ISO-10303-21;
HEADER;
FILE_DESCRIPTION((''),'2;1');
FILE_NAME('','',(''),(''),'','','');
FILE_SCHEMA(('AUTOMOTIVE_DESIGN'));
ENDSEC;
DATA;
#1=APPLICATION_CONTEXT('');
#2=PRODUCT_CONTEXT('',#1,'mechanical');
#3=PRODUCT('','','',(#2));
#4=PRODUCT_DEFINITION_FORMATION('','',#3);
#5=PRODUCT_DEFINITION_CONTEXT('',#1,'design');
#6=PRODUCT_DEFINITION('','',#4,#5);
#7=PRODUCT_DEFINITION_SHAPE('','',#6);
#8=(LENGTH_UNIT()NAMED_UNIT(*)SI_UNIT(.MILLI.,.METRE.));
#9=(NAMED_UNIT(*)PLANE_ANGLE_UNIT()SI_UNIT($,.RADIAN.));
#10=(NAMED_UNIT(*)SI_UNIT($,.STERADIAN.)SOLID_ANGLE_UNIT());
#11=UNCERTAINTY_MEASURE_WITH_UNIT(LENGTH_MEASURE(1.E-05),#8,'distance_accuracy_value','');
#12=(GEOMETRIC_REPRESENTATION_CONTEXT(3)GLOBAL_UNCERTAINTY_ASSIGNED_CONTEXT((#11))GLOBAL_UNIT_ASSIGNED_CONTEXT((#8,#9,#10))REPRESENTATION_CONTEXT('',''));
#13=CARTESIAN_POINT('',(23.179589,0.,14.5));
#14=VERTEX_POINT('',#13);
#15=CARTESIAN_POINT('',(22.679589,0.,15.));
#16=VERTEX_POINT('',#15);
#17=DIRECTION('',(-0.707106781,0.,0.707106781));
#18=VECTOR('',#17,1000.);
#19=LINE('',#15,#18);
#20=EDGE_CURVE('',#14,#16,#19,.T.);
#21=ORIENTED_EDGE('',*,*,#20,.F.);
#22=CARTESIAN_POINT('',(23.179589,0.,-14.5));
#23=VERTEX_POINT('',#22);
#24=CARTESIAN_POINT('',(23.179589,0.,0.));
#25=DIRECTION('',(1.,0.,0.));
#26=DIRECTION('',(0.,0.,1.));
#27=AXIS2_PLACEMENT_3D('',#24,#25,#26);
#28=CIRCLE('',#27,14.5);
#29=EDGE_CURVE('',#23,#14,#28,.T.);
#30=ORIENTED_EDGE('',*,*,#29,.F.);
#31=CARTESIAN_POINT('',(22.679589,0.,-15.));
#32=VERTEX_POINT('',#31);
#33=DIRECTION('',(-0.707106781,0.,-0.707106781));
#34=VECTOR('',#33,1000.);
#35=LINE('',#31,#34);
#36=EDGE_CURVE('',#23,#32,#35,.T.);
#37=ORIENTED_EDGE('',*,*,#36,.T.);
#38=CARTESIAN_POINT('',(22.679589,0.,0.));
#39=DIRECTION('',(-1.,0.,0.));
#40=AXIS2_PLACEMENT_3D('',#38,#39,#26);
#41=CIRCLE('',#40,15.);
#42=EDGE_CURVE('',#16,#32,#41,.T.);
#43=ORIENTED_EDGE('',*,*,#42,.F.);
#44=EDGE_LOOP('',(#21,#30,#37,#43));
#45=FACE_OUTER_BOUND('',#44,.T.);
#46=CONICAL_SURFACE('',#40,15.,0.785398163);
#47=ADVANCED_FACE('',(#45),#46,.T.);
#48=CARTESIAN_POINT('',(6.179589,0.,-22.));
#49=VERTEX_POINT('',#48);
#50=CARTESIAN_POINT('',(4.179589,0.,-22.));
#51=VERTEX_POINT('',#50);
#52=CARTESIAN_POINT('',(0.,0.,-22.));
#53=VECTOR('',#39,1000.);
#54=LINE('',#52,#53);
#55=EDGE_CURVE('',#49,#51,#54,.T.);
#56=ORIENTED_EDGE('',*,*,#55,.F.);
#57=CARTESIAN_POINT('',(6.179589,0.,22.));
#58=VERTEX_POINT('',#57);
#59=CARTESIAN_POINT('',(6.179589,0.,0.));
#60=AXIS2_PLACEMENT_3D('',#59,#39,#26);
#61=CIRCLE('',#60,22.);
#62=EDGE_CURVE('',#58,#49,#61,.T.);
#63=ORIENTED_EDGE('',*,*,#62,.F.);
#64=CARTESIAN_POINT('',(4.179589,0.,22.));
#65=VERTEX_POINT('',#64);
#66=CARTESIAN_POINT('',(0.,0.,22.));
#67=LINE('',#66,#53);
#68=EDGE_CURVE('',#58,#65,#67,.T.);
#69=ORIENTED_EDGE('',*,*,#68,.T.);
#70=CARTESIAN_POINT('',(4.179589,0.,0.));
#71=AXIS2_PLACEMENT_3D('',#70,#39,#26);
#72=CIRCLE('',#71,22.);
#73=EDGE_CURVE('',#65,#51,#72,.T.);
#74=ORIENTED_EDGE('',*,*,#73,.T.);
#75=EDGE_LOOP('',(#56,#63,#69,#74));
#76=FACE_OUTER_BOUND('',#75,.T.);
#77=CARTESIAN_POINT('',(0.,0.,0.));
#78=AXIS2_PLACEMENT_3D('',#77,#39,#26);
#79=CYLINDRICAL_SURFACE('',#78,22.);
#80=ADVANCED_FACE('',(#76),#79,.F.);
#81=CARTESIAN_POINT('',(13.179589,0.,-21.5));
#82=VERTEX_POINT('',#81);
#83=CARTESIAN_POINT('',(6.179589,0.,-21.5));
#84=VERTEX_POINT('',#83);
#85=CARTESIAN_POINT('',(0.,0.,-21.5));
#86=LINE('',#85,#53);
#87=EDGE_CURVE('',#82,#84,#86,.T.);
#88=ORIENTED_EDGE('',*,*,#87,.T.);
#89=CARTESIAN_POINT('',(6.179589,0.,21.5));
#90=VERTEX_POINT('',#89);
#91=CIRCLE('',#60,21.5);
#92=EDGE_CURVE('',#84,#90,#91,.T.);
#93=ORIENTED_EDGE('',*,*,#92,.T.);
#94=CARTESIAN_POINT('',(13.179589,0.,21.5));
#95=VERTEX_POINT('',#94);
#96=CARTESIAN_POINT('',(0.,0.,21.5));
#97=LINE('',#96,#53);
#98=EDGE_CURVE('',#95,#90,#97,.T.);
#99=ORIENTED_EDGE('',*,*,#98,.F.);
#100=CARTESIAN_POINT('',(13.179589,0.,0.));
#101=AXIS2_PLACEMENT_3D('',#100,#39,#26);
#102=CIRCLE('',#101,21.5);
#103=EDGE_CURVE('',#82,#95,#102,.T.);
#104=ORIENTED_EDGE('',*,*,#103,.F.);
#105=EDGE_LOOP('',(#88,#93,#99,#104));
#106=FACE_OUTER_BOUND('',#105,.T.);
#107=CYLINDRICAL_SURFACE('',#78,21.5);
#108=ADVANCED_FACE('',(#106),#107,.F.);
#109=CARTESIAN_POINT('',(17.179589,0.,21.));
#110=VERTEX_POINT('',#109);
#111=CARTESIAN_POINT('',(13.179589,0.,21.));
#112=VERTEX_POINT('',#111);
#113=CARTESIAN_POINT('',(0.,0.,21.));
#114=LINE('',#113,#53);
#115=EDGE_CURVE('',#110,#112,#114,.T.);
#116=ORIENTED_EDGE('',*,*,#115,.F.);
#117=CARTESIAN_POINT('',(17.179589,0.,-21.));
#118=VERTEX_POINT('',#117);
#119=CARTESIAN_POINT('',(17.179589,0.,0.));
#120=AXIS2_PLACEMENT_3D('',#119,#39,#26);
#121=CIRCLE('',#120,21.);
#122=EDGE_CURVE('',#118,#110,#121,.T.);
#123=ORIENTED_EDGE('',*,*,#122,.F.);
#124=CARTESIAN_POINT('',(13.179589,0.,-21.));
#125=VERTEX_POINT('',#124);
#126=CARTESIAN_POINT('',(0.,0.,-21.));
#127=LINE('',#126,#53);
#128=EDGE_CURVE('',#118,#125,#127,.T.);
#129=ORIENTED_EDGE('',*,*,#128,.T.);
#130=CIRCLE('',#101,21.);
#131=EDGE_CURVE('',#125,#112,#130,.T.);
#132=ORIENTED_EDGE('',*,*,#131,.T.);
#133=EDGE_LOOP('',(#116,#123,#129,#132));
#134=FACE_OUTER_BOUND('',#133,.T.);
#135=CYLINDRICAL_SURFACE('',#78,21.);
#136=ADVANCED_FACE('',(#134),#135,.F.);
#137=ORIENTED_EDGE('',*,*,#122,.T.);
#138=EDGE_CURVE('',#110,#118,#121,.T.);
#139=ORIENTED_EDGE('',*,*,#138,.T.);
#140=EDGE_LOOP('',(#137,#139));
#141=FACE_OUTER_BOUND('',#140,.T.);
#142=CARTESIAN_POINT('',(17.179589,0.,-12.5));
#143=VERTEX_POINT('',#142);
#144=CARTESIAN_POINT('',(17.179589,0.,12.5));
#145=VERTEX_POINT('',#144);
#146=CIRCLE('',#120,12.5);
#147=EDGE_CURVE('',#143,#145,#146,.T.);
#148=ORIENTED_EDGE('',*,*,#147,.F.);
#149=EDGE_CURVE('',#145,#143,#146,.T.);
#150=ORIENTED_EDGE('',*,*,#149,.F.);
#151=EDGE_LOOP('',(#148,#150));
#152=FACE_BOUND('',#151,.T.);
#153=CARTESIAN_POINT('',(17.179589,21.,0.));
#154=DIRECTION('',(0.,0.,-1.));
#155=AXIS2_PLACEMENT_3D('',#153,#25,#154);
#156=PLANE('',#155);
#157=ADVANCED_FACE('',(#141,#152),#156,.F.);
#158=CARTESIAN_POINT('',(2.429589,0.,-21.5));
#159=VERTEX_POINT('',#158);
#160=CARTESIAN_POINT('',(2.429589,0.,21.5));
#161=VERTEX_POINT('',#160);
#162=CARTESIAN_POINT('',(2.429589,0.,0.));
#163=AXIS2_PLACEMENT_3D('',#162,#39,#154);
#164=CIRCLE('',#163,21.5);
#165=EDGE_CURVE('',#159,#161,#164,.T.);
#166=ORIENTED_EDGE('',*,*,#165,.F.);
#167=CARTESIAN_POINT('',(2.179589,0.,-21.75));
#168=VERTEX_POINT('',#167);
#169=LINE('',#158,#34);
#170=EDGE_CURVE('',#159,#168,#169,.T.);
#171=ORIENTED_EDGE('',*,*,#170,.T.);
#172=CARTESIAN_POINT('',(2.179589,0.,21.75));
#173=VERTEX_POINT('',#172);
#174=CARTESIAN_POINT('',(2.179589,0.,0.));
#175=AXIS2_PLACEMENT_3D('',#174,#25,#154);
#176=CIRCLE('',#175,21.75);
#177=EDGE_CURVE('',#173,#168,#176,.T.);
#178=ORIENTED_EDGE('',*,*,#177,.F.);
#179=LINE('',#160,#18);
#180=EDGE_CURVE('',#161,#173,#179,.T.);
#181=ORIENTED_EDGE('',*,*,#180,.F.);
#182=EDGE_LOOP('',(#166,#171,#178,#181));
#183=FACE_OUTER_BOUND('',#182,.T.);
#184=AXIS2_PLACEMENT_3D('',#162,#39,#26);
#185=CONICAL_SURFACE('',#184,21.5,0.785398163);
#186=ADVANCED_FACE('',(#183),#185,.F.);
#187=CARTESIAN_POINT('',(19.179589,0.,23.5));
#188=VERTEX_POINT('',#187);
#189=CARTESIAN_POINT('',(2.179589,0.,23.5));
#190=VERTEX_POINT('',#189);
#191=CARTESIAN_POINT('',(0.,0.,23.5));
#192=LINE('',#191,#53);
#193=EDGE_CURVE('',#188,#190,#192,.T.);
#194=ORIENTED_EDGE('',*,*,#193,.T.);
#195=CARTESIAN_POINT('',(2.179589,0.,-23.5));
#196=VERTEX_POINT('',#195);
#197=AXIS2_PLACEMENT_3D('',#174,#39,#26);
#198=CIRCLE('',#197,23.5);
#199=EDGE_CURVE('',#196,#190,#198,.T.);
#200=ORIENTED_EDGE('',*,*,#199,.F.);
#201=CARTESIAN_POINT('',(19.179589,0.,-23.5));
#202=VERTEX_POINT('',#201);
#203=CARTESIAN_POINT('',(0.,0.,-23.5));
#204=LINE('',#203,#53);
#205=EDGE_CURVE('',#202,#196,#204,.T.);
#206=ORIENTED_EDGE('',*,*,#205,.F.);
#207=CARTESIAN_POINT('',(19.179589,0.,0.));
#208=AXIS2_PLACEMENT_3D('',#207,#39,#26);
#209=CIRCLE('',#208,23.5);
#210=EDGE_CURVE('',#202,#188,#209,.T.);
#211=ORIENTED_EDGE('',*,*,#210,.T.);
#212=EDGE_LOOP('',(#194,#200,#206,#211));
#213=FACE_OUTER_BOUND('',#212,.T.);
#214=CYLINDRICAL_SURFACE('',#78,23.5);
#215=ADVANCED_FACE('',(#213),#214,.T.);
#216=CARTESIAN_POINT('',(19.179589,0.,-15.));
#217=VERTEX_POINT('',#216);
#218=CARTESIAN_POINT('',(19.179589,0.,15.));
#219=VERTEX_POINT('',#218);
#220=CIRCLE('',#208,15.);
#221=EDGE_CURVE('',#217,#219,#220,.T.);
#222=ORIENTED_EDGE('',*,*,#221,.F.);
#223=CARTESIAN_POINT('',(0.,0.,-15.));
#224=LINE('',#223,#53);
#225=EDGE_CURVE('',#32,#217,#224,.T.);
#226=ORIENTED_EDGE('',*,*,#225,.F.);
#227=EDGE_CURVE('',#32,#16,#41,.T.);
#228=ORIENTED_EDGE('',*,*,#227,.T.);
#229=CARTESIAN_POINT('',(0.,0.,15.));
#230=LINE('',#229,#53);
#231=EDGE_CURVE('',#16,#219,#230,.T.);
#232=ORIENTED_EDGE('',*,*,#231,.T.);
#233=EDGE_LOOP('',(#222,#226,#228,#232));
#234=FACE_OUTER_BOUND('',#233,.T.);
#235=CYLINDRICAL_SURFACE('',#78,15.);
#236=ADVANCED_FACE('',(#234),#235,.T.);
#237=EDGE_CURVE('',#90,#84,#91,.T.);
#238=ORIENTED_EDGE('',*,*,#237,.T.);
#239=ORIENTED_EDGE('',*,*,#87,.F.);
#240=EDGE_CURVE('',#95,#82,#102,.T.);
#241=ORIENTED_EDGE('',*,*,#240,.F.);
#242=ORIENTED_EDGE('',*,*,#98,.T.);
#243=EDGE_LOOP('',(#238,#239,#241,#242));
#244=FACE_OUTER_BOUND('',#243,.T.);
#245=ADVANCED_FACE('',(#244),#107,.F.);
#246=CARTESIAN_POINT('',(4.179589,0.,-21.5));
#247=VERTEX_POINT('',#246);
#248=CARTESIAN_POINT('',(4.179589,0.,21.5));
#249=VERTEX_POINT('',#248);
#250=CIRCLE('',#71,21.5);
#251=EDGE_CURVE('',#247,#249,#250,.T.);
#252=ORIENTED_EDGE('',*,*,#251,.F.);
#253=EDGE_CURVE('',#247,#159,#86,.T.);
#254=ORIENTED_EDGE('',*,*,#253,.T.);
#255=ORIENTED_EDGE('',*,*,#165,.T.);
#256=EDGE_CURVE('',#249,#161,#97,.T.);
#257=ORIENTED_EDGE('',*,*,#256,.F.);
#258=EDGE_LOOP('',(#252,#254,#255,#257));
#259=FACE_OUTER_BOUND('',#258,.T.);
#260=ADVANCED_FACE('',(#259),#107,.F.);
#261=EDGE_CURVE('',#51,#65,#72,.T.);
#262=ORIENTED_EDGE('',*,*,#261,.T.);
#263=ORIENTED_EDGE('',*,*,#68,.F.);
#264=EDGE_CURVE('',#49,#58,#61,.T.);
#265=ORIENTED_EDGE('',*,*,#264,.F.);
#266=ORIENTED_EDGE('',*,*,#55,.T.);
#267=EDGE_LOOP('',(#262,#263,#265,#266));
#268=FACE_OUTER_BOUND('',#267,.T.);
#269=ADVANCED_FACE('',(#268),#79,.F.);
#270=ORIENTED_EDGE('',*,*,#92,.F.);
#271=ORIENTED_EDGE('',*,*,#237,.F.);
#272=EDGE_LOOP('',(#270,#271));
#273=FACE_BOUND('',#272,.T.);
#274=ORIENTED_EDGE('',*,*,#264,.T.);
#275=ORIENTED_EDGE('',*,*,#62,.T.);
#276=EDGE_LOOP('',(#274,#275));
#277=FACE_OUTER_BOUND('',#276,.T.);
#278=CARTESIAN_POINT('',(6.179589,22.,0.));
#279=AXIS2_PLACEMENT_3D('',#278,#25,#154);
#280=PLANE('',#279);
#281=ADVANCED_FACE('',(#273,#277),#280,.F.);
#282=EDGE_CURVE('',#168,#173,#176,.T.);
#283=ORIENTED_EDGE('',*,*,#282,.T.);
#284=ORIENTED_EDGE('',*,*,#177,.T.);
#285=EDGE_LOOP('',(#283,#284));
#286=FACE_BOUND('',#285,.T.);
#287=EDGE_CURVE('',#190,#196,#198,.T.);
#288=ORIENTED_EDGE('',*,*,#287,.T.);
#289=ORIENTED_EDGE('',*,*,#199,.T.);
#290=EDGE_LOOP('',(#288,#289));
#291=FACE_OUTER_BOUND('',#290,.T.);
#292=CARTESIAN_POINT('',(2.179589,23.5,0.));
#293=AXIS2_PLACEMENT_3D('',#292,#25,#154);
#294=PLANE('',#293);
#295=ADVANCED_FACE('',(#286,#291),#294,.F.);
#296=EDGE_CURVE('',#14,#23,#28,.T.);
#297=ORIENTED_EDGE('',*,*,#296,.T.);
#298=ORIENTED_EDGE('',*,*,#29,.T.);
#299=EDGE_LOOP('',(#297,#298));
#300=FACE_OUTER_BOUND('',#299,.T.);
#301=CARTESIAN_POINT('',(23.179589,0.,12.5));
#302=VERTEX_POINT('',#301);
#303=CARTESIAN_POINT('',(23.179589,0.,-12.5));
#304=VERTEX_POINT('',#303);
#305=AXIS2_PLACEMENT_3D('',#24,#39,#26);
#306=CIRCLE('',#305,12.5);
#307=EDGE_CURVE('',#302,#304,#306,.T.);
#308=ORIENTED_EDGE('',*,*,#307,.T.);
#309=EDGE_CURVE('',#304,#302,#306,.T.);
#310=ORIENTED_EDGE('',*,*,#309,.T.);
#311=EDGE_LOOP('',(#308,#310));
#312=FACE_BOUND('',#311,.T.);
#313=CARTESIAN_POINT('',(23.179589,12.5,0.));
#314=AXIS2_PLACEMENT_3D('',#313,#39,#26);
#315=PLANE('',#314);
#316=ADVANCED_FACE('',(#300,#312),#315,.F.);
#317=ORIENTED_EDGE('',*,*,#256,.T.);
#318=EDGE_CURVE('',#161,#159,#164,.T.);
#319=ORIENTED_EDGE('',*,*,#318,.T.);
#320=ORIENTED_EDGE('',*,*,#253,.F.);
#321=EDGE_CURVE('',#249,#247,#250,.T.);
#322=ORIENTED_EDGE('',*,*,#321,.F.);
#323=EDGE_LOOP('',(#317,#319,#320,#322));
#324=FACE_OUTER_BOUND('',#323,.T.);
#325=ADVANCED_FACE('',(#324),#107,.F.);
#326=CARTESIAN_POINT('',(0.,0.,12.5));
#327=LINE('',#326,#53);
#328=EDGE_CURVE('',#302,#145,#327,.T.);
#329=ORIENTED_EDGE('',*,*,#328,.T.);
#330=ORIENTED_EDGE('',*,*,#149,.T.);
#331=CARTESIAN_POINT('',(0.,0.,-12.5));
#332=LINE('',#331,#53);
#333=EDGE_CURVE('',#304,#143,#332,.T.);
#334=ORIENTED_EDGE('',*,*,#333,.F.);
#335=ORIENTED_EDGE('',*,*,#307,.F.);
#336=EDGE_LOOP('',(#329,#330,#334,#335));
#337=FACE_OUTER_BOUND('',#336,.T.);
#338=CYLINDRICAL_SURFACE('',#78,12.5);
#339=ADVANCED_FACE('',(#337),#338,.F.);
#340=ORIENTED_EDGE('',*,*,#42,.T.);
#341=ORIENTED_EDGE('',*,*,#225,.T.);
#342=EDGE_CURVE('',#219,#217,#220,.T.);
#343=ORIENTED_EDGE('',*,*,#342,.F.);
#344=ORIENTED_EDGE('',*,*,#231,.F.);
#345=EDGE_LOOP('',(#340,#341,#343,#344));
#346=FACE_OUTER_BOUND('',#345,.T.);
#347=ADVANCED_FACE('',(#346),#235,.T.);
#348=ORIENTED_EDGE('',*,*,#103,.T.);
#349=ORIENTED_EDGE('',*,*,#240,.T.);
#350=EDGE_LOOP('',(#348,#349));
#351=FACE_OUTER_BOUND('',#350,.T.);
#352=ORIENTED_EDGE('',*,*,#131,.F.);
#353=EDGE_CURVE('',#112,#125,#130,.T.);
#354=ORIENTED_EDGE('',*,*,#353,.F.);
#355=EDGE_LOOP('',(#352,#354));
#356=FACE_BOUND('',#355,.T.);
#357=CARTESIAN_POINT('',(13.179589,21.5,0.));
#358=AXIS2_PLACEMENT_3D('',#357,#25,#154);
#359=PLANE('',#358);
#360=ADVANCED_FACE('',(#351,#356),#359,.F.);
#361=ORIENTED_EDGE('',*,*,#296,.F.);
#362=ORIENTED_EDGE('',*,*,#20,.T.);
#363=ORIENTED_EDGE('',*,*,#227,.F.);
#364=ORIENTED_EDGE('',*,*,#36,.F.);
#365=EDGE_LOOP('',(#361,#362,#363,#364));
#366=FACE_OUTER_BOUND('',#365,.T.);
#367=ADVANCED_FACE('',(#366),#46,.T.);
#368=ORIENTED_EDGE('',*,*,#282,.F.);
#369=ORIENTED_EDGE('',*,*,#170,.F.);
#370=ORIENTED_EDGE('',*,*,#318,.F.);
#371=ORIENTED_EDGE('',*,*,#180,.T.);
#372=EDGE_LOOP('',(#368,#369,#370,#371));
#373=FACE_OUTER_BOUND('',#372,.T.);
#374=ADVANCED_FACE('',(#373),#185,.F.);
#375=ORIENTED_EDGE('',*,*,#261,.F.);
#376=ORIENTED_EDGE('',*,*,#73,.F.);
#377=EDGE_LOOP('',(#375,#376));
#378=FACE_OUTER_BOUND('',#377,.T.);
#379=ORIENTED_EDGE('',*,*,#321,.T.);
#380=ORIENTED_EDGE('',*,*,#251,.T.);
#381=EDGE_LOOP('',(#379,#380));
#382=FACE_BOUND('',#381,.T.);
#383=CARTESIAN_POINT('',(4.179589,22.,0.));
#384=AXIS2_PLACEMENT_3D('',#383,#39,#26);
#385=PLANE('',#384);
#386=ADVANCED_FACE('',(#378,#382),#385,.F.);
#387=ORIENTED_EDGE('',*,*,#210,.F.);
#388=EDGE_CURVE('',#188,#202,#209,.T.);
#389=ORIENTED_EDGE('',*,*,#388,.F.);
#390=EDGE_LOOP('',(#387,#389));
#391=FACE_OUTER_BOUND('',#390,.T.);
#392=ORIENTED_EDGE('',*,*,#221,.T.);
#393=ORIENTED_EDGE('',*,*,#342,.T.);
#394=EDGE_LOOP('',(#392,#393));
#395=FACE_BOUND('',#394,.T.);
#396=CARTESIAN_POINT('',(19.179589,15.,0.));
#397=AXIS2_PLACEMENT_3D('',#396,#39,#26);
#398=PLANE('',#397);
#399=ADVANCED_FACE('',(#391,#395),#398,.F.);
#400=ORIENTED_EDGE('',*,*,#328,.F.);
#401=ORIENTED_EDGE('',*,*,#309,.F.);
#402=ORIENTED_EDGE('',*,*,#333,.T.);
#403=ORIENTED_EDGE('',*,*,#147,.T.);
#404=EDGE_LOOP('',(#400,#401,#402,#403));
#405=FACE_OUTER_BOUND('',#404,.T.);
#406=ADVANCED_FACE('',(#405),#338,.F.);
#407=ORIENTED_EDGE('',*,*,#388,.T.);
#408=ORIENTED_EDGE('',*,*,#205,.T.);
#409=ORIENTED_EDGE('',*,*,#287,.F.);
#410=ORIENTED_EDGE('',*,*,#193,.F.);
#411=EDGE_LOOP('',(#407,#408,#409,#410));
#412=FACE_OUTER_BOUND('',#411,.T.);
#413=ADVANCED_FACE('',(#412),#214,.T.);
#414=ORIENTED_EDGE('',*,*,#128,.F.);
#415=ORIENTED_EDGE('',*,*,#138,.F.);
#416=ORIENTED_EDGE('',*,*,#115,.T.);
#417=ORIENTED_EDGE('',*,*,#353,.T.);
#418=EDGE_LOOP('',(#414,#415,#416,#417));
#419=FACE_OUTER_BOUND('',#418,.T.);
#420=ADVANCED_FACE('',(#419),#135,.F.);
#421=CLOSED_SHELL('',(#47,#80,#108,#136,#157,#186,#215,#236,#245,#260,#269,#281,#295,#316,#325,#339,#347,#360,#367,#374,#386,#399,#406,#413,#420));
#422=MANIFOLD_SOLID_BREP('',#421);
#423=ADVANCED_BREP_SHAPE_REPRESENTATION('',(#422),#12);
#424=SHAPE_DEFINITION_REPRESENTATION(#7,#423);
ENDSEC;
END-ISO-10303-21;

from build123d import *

# Parameters (mm, degrees)
CHAMFER_1_SIZE = 0.25
CHAMFER_2_SIZE = 0.5


with BuildPart() as part:
    # 草图1 → 旋转1 (revolve)
    with BuildSketch(Plane.XY, mode=Mode.PRIVATE) as revolve_1_sk:
        Polygon((2.179589421, 21.5), (4.179589421, 21.5), (4.179589421, 22), (6.179589421, 22), (6.179589421, 21.5), (13.179589421, 21.5), (13.179589421, 21), (17.179589421, 21), (17.179589421, 12.5), (23.179589421, 12.5), (23.179589421, 15), (19.179589421, 15), (19.179589421, 23.5), (2.179589421, 23.5), align=None)
    revolve(revolve_1_sk.sketch.rotate(Axis((0, 0, 0), (1, 0, 0)), 90), axis=Axis((0, 0, 0), (1, 0, 0)))

    # 倒角1
    chamfer_1_edges = [part.edges().sort_by_distance(p)[0] for p in [
        (2.179589421, 0, -21.5),
    ]]
    chamfer(chamfer_1_edges, length=CHAMFER_1_SIZE)

    # 倒角2
    chamfer_2_edges = [part.edges().sort_by_distance(p)[0] for p in [
        (23.179589421, 0, -15),
    ]]
    chamfer(chamfer_2_edges, length=CHAMFER_2_SIZE)


solid = part.part
